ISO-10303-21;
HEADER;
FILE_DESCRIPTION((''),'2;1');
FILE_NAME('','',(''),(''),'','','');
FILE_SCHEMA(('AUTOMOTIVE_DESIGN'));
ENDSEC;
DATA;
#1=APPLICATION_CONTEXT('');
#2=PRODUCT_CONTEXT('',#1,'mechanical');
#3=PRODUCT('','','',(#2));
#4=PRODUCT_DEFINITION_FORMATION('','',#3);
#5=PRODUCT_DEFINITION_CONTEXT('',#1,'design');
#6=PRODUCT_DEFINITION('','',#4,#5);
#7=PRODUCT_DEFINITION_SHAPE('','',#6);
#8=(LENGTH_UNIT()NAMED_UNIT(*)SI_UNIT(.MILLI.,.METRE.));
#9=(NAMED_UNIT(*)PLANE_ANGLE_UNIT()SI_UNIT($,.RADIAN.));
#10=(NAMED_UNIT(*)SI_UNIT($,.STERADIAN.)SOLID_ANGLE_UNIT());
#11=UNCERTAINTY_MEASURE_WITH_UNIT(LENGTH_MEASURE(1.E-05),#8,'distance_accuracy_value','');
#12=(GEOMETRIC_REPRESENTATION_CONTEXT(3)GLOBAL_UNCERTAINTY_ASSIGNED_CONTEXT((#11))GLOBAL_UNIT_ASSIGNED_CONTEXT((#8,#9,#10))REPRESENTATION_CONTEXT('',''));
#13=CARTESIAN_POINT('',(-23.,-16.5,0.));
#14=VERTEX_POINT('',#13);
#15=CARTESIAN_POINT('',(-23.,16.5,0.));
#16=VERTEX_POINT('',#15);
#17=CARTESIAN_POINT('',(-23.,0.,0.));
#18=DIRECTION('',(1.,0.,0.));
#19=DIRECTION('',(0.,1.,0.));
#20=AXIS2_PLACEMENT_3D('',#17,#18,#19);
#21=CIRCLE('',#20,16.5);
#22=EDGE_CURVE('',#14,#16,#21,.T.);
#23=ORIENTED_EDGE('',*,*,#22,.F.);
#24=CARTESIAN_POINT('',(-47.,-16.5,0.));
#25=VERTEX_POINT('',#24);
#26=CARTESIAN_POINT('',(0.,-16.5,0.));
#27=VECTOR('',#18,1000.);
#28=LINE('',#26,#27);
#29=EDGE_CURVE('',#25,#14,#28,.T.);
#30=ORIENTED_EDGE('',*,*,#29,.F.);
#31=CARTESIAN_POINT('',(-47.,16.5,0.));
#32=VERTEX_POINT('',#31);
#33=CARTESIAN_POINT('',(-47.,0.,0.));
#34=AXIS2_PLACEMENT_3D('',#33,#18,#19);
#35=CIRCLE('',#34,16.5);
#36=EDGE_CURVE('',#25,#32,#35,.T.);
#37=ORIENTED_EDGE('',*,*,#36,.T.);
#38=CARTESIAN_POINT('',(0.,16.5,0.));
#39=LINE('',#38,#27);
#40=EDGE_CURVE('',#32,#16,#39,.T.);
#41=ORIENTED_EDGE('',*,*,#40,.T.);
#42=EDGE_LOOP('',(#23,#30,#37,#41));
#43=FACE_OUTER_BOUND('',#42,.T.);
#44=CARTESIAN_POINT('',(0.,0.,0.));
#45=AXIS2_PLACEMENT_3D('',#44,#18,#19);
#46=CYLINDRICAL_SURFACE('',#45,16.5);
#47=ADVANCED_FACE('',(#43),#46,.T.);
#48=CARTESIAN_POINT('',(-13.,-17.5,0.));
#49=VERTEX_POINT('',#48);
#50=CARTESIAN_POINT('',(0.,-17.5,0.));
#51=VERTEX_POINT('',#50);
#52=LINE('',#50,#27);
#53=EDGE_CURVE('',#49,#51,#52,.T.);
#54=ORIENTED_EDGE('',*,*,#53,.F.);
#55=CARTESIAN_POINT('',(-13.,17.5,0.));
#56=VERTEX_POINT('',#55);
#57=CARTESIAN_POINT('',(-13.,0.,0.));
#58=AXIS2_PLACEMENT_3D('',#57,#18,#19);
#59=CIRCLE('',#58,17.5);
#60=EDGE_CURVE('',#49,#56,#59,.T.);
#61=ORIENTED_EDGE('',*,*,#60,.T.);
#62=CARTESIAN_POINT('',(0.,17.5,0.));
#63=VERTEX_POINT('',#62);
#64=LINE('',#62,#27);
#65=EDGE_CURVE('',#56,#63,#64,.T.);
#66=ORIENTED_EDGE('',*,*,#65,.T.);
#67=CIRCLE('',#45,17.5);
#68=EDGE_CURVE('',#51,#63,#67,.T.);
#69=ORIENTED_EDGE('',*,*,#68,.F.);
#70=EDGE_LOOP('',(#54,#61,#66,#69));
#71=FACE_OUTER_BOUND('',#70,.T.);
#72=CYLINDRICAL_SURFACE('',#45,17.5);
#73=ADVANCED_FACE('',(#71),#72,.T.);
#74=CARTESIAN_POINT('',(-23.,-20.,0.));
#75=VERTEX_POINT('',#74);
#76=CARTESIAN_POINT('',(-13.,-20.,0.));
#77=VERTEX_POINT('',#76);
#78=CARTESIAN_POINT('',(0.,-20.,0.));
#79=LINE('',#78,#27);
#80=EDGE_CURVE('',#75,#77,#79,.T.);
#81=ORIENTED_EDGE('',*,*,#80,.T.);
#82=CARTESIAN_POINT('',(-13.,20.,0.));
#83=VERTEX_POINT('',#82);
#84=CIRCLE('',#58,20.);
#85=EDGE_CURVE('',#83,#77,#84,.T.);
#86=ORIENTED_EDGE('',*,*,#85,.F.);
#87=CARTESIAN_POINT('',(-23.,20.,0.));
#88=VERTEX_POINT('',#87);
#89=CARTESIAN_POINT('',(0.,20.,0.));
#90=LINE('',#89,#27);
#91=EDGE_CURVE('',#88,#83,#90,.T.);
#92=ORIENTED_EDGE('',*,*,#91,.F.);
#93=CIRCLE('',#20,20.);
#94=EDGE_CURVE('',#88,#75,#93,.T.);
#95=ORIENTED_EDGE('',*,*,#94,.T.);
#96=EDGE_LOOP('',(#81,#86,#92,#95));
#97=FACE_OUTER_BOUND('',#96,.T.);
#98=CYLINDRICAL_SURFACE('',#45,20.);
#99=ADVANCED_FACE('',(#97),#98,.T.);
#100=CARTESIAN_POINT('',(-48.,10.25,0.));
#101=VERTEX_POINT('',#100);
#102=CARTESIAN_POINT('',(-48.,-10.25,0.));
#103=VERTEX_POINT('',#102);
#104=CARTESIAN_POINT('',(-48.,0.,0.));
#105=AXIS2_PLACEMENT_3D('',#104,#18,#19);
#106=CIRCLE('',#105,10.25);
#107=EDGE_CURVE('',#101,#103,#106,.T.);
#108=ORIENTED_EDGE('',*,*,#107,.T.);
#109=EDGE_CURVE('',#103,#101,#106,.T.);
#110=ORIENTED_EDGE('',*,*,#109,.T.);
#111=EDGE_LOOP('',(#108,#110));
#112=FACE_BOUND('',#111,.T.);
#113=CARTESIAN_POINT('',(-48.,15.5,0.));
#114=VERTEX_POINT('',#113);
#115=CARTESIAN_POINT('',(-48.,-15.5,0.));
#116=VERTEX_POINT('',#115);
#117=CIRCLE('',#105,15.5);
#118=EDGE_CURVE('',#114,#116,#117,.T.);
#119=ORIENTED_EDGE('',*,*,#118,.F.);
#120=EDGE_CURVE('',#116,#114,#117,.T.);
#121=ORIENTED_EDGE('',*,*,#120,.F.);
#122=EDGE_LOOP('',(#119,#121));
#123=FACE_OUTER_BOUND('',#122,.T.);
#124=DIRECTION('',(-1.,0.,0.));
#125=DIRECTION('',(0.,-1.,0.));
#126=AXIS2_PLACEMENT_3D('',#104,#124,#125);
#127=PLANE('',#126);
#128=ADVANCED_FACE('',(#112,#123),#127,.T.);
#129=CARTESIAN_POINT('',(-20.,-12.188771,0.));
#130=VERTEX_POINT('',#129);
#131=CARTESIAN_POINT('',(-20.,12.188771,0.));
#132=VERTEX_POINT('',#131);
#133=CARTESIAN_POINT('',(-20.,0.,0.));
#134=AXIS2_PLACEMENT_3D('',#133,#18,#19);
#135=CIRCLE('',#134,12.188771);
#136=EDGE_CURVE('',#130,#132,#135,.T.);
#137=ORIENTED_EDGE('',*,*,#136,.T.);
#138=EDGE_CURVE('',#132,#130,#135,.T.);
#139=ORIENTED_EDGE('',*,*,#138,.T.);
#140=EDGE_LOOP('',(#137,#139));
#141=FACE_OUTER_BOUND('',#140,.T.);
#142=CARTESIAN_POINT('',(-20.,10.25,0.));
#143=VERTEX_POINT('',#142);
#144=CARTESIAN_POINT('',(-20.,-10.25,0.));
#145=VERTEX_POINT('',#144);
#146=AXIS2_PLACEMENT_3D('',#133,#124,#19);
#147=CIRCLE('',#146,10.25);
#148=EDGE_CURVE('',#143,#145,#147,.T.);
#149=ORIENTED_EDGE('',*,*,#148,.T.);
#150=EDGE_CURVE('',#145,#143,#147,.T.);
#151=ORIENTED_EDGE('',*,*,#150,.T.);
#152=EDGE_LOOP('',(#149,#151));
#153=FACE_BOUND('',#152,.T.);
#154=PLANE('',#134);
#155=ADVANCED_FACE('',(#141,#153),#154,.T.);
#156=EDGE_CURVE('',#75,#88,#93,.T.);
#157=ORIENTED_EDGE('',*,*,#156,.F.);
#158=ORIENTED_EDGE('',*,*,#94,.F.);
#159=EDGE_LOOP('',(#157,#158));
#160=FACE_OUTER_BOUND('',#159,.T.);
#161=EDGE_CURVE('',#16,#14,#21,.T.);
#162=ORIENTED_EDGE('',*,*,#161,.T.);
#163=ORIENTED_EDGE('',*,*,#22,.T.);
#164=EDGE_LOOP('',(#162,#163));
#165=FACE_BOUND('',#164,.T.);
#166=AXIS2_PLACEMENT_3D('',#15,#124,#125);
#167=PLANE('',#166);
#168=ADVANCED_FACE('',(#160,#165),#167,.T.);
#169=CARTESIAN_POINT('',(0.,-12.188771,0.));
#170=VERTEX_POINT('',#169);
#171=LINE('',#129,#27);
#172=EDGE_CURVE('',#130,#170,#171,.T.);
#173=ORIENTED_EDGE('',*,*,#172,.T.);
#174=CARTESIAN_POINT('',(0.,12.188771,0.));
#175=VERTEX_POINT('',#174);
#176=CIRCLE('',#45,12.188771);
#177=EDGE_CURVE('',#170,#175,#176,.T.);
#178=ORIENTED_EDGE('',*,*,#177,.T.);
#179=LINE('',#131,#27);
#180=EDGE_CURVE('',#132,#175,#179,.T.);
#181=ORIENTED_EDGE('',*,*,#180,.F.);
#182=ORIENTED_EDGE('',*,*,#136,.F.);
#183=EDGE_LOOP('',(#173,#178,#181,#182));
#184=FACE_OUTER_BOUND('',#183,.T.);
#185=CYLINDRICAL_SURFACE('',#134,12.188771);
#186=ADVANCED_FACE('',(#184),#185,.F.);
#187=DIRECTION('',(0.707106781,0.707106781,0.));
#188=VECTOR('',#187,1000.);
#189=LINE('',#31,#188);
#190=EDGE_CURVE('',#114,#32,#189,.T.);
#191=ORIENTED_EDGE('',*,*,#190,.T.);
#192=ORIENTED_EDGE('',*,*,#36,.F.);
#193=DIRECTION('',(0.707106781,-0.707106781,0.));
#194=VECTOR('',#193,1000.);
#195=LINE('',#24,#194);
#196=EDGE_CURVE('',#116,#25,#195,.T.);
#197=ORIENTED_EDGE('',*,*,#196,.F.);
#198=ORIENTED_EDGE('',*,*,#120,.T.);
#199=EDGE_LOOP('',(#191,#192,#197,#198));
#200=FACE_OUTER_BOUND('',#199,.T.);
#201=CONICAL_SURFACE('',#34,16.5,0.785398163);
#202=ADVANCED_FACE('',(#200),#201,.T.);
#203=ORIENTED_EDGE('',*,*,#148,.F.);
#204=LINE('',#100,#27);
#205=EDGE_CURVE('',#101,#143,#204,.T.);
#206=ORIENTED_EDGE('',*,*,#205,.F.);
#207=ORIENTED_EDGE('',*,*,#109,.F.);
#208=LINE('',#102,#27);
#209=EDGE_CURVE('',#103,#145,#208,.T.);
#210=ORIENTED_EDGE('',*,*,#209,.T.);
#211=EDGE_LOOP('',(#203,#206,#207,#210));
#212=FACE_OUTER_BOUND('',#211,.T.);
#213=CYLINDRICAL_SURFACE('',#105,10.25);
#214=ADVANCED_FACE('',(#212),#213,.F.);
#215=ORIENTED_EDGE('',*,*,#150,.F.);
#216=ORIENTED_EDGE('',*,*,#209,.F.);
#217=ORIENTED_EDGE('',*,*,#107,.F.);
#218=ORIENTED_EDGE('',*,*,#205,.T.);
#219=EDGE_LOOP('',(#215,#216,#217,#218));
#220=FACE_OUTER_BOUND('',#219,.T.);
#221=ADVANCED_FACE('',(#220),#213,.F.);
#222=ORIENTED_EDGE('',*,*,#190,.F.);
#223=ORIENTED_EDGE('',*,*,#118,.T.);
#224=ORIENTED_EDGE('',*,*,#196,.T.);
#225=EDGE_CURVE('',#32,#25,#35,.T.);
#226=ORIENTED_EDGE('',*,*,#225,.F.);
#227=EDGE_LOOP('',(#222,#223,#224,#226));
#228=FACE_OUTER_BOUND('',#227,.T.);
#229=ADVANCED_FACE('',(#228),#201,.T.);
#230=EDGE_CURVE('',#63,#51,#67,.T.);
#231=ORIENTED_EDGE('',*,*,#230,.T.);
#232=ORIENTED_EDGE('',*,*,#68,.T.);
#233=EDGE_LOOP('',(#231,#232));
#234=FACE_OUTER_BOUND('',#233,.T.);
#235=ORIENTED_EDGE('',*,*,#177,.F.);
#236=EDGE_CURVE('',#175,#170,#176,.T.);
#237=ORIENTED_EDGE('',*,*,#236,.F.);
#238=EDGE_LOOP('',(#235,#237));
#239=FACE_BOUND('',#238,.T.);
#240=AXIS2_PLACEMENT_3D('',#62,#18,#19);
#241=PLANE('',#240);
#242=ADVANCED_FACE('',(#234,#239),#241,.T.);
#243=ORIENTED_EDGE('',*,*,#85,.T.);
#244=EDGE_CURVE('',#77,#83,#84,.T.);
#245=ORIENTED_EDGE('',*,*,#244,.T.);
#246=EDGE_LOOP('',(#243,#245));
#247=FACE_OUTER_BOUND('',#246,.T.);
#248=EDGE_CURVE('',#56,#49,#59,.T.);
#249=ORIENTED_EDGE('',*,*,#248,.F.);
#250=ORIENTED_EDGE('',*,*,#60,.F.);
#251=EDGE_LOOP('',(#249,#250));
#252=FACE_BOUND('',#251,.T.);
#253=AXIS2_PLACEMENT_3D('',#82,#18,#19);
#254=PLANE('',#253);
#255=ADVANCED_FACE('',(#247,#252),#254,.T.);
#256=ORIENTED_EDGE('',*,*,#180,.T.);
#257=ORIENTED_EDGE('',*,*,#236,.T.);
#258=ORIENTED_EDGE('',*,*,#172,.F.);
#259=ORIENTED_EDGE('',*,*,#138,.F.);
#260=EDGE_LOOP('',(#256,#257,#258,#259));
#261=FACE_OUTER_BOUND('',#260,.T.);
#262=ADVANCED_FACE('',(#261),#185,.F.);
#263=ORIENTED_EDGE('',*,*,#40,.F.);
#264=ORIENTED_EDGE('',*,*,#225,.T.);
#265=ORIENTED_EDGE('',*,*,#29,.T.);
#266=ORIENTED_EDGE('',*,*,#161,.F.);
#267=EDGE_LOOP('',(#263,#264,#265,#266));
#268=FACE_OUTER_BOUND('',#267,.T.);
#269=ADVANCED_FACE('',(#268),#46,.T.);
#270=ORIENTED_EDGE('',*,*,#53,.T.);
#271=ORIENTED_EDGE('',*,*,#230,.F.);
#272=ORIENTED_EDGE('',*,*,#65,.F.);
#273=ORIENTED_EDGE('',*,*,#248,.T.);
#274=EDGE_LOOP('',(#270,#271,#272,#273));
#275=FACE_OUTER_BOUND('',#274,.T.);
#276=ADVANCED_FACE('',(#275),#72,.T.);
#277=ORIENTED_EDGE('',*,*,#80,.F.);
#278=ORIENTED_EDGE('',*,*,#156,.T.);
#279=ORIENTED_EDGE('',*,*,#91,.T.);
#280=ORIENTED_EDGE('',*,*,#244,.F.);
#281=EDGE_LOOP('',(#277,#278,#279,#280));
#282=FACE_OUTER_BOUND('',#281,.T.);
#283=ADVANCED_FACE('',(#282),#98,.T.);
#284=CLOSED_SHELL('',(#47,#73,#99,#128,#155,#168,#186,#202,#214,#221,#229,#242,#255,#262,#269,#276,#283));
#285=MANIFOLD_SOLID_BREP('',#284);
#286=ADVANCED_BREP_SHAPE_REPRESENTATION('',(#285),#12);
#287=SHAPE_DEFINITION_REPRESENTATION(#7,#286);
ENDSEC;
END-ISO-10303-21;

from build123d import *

# Parameters (mm, degrees)
SKETCH2_R          = 10.25
CUT_EXTRUDE1_DEPTH = 56.713553109
SKETCH4_R          = 12.188770661
CUT_EXTRUDE2_DEPTH = 20


with BuildPart() as part:
    # Sketch1 → Revolve1 (revolve)
    with BuildSketch(Plane.XY):
        Polygon((-48, 0), (-48, 15.5), (-47, 16.5), (-23, 16.5), (-23, 20), (-13, 20), (-13, 17.5), (0, 17.5), (0, 0), align=None)
    revolve(axis=Axis((0, 0, 0), (-1, 0, 0)))

    # Sketch2 → Cut-Extrude1 (cut, through all)
    with BuildSketch(Plane(origin=(0, 0, 0), x_dir=(0, 0, -1), z_dir=(1, 0, 0))):
        with Locations(Location((0, 0, 0), (0, 0, 90))):
            Circle(SKETCH2_R)
    extrude(amount=-CUT_EXTRUDE1_DEPTH, mode=Mode.SUBTRACT)

    # Sketch4 → Cut-Extrude2 (cut)
    with BuildSketch(Plane(origin=(0, 0, 0), x_dir=(0, 0, -1), z_dir=(1, 0, 0))):
        with Locations(Location((0, 0, 0), (0, 0, 90))):
            Circle(SKETCH4_R)
    extrude(amount=-CUT_EXTRUDE2_DEPTH, mode=Mode.SUBTRACT)


solid = part.part
